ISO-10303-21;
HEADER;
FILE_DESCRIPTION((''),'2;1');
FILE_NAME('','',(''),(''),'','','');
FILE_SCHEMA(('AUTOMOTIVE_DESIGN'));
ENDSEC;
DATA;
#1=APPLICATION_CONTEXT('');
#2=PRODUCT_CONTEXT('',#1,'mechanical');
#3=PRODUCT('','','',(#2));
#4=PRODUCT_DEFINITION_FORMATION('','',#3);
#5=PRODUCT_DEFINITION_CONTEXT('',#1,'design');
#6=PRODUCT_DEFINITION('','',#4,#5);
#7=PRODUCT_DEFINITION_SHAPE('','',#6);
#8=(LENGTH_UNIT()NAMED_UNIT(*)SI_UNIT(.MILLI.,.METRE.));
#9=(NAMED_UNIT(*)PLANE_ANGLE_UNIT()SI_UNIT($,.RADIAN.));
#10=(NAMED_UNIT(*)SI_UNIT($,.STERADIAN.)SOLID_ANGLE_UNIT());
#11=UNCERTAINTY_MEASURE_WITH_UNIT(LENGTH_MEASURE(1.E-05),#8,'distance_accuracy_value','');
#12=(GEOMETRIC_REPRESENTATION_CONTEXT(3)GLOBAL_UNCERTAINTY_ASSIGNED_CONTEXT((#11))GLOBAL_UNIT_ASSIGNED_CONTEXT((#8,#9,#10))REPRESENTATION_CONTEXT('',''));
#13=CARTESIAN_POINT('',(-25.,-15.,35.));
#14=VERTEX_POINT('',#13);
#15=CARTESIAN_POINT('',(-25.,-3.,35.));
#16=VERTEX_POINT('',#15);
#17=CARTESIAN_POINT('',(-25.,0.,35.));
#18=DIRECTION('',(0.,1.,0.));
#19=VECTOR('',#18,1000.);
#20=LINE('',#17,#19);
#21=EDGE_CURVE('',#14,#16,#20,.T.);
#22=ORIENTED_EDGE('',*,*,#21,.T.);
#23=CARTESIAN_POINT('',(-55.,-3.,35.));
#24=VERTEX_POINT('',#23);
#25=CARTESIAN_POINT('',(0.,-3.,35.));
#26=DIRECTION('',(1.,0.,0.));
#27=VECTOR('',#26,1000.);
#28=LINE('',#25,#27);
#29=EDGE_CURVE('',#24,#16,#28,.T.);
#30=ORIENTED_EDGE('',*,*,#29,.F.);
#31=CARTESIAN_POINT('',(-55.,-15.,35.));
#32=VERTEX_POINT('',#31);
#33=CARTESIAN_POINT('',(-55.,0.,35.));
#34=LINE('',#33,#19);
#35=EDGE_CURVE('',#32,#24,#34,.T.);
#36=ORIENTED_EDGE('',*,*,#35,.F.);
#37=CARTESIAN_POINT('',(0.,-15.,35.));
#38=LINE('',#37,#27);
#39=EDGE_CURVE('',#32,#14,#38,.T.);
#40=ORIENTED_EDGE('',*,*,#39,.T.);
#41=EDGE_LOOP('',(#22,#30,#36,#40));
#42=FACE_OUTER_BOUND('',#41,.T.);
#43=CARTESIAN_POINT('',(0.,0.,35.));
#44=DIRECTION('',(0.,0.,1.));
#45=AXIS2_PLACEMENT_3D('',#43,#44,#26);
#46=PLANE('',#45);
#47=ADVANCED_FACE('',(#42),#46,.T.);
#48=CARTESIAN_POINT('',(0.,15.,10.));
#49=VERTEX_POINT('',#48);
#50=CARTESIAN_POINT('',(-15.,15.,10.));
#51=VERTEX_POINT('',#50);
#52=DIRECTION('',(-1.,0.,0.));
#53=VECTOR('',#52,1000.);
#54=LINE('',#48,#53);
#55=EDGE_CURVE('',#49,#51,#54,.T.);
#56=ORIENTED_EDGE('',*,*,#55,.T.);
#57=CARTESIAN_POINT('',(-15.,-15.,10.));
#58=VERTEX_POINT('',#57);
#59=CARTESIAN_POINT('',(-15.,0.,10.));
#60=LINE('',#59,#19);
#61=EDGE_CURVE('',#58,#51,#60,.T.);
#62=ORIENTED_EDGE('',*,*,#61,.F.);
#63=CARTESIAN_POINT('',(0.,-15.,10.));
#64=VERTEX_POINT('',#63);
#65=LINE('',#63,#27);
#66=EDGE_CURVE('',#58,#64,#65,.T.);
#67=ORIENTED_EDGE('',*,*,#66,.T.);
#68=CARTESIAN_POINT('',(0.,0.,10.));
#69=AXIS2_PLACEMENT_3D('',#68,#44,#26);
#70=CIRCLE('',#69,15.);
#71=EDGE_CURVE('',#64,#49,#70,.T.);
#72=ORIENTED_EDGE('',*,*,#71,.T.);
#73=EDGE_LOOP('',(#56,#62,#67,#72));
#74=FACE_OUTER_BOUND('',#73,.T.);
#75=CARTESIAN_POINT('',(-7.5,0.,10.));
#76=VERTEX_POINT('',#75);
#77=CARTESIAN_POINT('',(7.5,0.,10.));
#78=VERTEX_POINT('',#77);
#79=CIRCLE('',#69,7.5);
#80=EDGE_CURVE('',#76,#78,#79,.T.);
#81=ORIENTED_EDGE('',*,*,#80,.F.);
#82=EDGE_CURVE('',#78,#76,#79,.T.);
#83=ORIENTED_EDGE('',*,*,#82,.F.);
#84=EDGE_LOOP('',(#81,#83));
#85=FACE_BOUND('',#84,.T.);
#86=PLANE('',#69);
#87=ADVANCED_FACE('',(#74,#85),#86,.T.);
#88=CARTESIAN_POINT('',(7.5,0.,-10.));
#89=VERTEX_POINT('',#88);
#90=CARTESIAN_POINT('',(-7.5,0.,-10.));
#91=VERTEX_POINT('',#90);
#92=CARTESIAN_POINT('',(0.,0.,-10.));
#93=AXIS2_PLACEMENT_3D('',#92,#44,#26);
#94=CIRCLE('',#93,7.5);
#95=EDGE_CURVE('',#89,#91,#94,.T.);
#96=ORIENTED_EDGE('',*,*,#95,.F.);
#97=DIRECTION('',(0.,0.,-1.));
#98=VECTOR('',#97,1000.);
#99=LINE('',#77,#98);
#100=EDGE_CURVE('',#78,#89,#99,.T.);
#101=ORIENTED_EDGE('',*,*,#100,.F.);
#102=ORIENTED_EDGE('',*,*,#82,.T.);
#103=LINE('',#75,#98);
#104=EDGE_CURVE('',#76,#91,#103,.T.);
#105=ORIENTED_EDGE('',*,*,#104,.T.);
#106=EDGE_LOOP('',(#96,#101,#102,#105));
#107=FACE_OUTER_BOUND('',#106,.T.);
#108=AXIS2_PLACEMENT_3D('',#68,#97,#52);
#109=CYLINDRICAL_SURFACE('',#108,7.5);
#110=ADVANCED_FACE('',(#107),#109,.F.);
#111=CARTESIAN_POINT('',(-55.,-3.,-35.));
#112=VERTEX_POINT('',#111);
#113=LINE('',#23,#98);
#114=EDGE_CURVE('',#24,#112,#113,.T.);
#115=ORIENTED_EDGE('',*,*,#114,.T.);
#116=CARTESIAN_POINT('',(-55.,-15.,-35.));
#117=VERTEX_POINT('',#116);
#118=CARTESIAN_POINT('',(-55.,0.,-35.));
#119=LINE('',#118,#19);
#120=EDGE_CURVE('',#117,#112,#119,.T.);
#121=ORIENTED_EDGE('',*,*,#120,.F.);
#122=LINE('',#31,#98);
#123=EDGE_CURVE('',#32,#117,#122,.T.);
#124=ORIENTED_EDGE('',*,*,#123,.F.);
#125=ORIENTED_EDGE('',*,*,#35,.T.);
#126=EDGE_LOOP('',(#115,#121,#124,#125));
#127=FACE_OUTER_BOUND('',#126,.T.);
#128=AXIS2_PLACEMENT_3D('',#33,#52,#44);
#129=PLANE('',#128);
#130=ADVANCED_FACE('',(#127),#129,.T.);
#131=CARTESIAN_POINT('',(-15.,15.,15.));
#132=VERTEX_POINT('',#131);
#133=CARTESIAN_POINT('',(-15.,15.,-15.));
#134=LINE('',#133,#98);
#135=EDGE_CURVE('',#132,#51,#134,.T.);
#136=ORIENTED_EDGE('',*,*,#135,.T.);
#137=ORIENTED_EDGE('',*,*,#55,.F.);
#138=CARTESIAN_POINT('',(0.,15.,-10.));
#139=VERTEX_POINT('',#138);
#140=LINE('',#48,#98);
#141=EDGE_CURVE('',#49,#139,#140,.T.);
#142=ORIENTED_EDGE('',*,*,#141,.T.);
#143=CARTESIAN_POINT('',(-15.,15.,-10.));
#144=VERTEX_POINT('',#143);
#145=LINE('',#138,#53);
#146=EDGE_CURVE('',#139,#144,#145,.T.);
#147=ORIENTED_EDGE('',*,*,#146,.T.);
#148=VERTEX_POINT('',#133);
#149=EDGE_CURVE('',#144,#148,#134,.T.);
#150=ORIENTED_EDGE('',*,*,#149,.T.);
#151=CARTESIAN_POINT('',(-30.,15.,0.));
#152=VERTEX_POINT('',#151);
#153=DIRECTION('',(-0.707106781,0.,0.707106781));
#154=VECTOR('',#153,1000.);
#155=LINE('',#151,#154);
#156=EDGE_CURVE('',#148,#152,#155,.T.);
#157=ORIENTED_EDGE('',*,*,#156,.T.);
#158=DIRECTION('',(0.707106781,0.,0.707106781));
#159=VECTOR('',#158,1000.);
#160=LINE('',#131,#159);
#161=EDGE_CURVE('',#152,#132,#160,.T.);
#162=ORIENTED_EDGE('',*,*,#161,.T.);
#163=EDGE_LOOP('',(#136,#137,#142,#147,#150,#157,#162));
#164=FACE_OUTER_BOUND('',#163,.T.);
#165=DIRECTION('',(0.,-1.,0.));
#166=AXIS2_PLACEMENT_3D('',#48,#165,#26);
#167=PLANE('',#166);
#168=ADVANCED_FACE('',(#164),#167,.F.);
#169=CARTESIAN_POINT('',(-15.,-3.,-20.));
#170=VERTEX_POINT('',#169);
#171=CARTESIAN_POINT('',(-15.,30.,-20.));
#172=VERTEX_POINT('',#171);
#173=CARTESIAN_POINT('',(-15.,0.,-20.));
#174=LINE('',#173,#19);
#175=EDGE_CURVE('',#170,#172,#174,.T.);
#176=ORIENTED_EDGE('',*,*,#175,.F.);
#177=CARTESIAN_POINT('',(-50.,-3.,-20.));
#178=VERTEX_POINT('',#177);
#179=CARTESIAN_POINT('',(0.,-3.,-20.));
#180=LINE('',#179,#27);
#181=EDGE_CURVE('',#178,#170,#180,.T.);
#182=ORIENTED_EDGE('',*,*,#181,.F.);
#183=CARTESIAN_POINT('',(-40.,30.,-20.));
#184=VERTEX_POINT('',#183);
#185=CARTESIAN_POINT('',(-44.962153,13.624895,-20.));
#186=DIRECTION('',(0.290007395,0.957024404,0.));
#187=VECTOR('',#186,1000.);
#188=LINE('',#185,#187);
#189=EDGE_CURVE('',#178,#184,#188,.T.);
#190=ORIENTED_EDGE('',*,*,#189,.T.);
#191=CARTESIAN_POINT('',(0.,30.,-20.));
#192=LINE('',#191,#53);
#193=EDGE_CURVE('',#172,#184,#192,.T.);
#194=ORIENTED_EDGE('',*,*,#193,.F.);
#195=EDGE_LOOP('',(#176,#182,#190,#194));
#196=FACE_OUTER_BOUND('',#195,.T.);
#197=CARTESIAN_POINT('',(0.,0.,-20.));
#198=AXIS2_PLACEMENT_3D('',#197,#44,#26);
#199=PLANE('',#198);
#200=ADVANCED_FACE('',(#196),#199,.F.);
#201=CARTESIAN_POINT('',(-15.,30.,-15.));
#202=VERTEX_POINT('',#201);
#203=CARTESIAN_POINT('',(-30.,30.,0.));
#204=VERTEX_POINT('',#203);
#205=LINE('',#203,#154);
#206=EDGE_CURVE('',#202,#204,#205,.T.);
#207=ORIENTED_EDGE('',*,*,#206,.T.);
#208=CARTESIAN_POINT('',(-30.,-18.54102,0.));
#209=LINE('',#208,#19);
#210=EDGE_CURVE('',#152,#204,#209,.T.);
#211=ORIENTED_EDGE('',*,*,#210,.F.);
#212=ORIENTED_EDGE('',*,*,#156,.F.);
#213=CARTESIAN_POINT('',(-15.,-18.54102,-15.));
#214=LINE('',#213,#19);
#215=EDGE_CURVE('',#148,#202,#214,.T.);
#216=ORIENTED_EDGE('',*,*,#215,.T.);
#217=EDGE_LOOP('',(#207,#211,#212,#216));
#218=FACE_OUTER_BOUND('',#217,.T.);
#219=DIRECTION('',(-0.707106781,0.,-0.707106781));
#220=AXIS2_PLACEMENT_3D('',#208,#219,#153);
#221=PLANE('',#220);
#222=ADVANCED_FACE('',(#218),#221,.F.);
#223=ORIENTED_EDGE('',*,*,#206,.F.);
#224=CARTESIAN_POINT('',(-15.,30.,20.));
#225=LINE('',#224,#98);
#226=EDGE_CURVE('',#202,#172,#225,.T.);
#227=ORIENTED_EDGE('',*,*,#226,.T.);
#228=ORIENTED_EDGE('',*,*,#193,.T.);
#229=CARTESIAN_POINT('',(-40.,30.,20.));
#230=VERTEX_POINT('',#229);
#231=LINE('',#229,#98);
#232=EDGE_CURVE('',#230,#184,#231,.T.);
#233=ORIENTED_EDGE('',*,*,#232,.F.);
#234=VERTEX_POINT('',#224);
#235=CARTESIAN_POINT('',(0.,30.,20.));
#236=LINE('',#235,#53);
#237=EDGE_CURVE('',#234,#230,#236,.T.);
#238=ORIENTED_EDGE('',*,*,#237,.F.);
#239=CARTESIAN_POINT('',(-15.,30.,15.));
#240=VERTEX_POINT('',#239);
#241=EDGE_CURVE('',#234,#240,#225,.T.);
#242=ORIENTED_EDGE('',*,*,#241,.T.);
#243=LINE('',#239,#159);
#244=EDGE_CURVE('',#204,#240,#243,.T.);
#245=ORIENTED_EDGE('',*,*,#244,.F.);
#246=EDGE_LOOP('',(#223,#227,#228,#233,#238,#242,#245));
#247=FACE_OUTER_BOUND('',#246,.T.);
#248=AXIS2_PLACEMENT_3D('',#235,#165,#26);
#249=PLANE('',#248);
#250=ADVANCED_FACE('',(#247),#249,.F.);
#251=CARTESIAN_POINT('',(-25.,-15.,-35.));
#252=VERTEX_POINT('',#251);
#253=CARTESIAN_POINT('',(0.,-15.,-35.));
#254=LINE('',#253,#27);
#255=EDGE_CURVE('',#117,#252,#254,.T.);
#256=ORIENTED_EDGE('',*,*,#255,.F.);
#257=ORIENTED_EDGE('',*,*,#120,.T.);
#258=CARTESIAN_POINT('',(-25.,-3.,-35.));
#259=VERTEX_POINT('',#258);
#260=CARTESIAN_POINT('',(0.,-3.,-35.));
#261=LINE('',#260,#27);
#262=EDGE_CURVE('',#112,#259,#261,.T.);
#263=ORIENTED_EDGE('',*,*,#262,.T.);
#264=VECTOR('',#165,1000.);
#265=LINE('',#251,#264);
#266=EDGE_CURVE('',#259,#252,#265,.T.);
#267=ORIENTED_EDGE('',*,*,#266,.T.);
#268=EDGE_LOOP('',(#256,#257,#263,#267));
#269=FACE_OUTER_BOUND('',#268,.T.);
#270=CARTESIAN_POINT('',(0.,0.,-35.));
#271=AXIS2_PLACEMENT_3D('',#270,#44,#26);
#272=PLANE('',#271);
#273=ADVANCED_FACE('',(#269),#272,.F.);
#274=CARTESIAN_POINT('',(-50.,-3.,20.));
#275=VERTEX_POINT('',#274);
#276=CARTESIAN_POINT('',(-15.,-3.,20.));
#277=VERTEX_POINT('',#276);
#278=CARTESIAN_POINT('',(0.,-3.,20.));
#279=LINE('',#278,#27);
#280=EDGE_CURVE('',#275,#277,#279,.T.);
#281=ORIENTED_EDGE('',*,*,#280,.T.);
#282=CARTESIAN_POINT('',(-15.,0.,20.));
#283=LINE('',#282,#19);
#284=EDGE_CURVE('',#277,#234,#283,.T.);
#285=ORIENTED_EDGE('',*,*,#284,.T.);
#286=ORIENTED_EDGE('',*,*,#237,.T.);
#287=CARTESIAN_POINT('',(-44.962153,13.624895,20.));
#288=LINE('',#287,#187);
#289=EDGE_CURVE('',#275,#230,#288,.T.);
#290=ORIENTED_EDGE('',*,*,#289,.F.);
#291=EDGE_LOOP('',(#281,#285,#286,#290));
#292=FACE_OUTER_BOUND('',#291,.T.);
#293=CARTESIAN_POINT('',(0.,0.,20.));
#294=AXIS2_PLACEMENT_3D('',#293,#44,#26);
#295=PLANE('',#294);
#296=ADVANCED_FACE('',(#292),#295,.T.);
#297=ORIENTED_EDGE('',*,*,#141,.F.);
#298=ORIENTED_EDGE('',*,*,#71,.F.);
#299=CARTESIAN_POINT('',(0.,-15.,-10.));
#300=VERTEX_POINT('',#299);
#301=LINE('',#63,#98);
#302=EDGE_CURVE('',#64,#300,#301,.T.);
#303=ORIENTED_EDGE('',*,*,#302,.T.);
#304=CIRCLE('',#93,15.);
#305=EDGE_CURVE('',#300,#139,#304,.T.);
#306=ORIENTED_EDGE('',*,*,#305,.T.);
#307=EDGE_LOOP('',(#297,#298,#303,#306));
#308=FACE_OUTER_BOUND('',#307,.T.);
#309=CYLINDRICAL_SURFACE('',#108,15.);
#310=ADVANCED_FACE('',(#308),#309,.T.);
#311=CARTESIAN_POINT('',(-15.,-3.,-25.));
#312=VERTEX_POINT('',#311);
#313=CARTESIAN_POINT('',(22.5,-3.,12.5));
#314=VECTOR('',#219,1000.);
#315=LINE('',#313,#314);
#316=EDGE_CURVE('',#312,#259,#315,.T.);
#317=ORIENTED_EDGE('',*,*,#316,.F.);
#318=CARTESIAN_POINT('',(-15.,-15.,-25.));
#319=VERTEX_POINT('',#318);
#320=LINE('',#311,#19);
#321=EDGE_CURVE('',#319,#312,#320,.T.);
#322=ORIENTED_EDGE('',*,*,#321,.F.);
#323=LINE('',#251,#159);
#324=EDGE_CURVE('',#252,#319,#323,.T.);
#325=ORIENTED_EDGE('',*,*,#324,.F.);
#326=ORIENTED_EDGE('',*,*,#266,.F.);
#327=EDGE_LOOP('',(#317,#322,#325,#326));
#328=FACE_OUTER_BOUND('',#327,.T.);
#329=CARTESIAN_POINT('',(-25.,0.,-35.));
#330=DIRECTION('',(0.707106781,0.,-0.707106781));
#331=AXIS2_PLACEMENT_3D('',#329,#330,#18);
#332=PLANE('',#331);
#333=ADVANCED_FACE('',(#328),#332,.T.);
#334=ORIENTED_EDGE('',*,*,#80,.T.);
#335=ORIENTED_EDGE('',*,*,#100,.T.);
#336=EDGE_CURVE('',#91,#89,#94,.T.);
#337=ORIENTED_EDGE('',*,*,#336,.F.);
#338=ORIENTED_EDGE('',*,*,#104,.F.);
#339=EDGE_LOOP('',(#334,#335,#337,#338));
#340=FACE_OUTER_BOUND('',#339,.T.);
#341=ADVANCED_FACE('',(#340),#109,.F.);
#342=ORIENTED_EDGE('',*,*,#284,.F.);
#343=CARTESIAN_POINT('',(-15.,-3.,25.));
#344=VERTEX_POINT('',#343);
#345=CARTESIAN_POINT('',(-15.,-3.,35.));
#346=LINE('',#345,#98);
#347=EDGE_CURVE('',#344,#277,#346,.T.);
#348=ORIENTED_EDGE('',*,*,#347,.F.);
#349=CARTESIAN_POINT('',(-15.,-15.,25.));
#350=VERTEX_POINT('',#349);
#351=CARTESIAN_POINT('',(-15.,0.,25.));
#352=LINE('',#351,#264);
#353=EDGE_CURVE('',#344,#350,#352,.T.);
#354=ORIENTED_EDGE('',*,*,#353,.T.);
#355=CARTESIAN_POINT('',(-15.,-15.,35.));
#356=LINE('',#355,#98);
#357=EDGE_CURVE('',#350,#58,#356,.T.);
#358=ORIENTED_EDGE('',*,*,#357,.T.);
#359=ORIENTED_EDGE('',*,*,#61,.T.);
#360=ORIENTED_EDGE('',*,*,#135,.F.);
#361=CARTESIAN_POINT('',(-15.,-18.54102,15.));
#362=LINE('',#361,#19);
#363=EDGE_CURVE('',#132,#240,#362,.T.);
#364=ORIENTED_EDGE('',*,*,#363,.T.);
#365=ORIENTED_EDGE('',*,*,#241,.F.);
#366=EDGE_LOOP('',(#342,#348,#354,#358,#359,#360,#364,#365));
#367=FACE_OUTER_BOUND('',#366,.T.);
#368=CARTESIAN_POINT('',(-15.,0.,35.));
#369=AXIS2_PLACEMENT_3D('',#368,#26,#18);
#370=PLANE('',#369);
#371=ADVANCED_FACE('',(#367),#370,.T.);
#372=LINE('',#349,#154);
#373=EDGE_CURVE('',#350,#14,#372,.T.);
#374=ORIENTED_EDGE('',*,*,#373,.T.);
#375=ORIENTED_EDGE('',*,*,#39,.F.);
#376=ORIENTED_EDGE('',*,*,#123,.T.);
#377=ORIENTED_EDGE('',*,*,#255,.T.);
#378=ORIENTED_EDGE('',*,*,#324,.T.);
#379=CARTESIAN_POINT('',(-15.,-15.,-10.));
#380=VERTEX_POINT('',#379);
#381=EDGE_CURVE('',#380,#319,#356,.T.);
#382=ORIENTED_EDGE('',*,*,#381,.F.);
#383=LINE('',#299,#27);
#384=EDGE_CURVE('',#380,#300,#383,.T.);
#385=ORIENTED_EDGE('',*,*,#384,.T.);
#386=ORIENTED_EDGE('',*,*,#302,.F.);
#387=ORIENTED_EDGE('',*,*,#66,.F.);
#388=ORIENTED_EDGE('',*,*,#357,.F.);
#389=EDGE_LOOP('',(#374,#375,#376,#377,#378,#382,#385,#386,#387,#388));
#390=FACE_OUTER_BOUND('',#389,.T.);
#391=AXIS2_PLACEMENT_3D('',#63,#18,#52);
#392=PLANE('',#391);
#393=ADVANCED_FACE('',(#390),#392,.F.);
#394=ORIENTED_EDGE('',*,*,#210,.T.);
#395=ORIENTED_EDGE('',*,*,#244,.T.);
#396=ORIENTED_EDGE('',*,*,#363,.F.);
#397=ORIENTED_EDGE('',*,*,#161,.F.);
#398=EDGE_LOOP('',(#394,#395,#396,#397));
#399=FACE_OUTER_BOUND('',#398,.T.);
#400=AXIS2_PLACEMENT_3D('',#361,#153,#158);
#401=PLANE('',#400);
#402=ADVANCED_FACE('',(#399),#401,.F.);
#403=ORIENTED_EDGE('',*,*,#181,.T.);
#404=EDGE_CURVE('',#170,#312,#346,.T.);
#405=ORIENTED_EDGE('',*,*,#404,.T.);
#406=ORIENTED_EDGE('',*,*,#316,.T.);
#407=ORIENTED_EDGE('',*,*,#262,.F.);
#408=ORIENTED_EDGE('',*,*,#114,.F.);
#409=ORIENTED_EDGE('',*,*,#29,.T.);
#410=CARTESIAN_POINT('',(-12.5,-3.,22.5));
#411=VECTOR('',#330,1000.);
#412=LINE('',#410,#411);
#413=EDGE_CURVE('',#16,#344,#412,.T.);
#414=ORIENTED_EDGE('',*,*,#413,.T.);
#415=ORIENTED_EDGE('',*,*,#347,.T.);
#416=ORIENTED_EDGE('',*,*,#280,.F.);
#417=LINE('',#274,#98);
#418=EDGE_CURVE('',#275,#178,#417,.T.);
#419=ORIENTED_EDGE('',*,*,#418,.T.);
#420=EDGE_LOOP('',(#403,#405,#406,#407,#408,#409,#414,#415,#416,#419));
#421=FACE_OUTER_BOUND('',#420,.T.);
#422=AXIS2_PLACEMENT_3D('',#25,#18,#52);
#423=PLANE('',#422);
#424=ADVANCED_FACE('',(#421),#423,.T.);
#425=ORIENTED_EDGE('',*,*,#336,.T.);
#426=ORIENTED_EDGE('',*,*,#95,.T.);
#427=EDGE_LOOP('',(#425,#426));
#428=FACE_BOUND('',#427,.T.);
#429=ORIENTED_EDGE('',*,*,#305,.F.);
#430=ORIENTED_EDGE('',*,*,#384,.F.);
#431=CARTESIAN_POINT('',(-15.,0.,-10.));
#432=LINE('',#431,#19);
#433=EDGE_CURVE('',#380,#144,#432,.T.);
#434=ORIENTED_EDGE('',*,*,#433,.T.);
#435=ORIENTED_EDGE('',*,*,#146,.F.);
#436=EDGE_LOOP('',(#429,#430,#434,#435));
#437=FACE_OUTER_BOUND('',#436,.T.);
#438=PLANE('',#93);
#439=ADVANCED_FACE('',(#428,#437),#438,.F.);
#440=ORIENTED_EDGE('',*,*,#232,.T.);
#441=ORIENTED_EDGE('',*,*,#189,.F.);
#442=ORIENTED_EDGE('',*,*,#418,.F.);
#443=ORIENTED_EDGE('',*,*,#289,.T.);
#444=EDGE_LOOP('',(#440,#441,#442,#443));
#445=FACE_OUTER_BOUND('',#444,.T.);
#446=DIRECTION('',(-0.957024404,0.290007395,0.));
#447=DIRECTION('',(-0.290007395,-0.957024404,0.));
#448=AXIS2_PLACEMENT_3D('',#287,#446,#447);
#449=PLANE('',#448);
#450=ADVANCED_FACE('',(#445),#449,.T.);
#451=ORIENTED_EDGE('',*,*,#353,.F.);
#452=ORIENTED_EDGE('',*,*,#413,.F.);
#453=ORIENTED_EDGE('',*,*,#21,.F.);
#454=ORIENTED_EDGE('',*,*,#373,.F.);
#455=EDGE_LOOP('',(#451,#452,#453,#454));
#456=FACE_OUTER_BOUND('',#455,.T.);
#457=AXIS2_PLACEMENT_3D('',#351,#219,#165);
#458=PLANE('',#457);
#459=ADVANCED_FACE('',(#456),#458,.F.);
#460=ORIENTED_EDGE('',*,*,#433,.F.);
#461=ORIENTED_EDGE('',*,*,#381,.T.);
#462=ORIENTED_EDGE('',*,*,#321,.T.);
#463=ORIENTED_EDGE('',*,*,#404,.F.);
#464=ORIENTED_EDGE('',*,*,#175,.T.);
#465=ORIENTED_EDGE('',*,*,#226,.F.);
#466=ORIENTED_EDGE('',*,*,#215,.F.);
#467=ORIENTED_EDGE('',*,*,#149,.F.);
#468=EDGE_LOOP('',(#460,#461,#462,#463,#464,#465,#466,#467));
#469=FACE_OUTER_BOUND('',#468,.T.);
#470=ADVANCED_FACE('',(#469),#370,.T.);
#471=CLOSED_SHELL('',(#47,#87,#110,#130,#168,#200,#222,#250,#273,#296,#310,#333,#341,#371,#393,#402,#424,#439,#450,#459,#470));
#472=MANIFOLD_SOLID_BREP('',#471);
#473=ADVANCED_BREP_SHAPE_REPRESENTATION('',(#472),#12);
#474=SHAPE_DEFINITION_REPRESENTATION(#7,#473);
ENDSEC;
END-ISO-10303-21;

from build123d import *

# Parameters (mm, degrees)
BRACKET_PROFILE_SKETCH_R       = 7.5
LUG_EYE_BOSS_20MM_DEPTH        = 10
SKETCH5_3_W                    = 40
SKETCH5_3_H                    = 12
BASE_BLOCK_70MM_DEPTH          = 35
UPRIGHT_BLOCK_40MM_DEPTH       = 20
UPRIGHT_EDGE_CHAMFER_10MM_SIZE = 10
FORK_SLOT_CUT_30X15_DEPTH      = 15


with BuildPart() as part:
    # Bracket Profile Sketch → Lug Eye Boss 20mm (new, symmetric)
    with BuildSketch(Plane.XY):
        with BuildLine():
            Line((-15, -3), (-15, -15))
            Line((-15, -15), (0, -15))
            ThreePointArc((0, -15), (15, 0), (0, 15))
            Line((0, 15), (-15, 15))
            Line((-15, 15), (-15, -3))
        make_face()
        Circle(BRACKET_PROFILE_SKETCH_R, mode=Mode.SUBTRACT)
    extrude(amount=LUG_EYE_BOSS_20MM_DEPTH, both=True)

    # Sketch5_3 → Base Block 70mm (add, symmetric)
    with BuildSketch(Plane.XY):
        with Locations((-35, -9)):
            Rectangle(SKETCH5_3_W, SKETCH5_3_H)
    extrude(amount=BASE_BLOCK_70MM_DEPTH, both=True)

    # Sketch5_4 → Upright Block 40mm (add, symmetric)
    with BuildSketch(Plane.XY):
        Polygon((-50, -3), (-15, -3), (-15, 15), (-15, 30), (-40, 30), align=None)
    extrude(amount=UPRIGHT_BLOCK_40MM_DEPTH, both=True)

    # Upright Edge Chamfer 10mm
    upright_edge_chamfer_10mm_edges = [part.edges().sort_by_distance(p)[0] for p in [
        (-15, -9, -35),
        (-15, -9, 35),
    ]]
    chamfer(upright_edge_chamfer_10mm_edges, length=UPRIGHT_EDGE_CHAMFER_10MM_SIZE)

    # Fork Slot Sketch → Fork Slot Cut 30x15 (cut)
    with BuildSketch(Plane(origin=(0, 30, 0), x_dir=(1, 0, 0), z_dir=(0, 1, 0))):
        Polygon((-15, -15), (-30, 0), (-15, 15), align=None)
    extrude(amount=-FORK_SLOT_CUT_30X15_DEPTH, mode=Mode.SUBTRACT)


solid = part.part
